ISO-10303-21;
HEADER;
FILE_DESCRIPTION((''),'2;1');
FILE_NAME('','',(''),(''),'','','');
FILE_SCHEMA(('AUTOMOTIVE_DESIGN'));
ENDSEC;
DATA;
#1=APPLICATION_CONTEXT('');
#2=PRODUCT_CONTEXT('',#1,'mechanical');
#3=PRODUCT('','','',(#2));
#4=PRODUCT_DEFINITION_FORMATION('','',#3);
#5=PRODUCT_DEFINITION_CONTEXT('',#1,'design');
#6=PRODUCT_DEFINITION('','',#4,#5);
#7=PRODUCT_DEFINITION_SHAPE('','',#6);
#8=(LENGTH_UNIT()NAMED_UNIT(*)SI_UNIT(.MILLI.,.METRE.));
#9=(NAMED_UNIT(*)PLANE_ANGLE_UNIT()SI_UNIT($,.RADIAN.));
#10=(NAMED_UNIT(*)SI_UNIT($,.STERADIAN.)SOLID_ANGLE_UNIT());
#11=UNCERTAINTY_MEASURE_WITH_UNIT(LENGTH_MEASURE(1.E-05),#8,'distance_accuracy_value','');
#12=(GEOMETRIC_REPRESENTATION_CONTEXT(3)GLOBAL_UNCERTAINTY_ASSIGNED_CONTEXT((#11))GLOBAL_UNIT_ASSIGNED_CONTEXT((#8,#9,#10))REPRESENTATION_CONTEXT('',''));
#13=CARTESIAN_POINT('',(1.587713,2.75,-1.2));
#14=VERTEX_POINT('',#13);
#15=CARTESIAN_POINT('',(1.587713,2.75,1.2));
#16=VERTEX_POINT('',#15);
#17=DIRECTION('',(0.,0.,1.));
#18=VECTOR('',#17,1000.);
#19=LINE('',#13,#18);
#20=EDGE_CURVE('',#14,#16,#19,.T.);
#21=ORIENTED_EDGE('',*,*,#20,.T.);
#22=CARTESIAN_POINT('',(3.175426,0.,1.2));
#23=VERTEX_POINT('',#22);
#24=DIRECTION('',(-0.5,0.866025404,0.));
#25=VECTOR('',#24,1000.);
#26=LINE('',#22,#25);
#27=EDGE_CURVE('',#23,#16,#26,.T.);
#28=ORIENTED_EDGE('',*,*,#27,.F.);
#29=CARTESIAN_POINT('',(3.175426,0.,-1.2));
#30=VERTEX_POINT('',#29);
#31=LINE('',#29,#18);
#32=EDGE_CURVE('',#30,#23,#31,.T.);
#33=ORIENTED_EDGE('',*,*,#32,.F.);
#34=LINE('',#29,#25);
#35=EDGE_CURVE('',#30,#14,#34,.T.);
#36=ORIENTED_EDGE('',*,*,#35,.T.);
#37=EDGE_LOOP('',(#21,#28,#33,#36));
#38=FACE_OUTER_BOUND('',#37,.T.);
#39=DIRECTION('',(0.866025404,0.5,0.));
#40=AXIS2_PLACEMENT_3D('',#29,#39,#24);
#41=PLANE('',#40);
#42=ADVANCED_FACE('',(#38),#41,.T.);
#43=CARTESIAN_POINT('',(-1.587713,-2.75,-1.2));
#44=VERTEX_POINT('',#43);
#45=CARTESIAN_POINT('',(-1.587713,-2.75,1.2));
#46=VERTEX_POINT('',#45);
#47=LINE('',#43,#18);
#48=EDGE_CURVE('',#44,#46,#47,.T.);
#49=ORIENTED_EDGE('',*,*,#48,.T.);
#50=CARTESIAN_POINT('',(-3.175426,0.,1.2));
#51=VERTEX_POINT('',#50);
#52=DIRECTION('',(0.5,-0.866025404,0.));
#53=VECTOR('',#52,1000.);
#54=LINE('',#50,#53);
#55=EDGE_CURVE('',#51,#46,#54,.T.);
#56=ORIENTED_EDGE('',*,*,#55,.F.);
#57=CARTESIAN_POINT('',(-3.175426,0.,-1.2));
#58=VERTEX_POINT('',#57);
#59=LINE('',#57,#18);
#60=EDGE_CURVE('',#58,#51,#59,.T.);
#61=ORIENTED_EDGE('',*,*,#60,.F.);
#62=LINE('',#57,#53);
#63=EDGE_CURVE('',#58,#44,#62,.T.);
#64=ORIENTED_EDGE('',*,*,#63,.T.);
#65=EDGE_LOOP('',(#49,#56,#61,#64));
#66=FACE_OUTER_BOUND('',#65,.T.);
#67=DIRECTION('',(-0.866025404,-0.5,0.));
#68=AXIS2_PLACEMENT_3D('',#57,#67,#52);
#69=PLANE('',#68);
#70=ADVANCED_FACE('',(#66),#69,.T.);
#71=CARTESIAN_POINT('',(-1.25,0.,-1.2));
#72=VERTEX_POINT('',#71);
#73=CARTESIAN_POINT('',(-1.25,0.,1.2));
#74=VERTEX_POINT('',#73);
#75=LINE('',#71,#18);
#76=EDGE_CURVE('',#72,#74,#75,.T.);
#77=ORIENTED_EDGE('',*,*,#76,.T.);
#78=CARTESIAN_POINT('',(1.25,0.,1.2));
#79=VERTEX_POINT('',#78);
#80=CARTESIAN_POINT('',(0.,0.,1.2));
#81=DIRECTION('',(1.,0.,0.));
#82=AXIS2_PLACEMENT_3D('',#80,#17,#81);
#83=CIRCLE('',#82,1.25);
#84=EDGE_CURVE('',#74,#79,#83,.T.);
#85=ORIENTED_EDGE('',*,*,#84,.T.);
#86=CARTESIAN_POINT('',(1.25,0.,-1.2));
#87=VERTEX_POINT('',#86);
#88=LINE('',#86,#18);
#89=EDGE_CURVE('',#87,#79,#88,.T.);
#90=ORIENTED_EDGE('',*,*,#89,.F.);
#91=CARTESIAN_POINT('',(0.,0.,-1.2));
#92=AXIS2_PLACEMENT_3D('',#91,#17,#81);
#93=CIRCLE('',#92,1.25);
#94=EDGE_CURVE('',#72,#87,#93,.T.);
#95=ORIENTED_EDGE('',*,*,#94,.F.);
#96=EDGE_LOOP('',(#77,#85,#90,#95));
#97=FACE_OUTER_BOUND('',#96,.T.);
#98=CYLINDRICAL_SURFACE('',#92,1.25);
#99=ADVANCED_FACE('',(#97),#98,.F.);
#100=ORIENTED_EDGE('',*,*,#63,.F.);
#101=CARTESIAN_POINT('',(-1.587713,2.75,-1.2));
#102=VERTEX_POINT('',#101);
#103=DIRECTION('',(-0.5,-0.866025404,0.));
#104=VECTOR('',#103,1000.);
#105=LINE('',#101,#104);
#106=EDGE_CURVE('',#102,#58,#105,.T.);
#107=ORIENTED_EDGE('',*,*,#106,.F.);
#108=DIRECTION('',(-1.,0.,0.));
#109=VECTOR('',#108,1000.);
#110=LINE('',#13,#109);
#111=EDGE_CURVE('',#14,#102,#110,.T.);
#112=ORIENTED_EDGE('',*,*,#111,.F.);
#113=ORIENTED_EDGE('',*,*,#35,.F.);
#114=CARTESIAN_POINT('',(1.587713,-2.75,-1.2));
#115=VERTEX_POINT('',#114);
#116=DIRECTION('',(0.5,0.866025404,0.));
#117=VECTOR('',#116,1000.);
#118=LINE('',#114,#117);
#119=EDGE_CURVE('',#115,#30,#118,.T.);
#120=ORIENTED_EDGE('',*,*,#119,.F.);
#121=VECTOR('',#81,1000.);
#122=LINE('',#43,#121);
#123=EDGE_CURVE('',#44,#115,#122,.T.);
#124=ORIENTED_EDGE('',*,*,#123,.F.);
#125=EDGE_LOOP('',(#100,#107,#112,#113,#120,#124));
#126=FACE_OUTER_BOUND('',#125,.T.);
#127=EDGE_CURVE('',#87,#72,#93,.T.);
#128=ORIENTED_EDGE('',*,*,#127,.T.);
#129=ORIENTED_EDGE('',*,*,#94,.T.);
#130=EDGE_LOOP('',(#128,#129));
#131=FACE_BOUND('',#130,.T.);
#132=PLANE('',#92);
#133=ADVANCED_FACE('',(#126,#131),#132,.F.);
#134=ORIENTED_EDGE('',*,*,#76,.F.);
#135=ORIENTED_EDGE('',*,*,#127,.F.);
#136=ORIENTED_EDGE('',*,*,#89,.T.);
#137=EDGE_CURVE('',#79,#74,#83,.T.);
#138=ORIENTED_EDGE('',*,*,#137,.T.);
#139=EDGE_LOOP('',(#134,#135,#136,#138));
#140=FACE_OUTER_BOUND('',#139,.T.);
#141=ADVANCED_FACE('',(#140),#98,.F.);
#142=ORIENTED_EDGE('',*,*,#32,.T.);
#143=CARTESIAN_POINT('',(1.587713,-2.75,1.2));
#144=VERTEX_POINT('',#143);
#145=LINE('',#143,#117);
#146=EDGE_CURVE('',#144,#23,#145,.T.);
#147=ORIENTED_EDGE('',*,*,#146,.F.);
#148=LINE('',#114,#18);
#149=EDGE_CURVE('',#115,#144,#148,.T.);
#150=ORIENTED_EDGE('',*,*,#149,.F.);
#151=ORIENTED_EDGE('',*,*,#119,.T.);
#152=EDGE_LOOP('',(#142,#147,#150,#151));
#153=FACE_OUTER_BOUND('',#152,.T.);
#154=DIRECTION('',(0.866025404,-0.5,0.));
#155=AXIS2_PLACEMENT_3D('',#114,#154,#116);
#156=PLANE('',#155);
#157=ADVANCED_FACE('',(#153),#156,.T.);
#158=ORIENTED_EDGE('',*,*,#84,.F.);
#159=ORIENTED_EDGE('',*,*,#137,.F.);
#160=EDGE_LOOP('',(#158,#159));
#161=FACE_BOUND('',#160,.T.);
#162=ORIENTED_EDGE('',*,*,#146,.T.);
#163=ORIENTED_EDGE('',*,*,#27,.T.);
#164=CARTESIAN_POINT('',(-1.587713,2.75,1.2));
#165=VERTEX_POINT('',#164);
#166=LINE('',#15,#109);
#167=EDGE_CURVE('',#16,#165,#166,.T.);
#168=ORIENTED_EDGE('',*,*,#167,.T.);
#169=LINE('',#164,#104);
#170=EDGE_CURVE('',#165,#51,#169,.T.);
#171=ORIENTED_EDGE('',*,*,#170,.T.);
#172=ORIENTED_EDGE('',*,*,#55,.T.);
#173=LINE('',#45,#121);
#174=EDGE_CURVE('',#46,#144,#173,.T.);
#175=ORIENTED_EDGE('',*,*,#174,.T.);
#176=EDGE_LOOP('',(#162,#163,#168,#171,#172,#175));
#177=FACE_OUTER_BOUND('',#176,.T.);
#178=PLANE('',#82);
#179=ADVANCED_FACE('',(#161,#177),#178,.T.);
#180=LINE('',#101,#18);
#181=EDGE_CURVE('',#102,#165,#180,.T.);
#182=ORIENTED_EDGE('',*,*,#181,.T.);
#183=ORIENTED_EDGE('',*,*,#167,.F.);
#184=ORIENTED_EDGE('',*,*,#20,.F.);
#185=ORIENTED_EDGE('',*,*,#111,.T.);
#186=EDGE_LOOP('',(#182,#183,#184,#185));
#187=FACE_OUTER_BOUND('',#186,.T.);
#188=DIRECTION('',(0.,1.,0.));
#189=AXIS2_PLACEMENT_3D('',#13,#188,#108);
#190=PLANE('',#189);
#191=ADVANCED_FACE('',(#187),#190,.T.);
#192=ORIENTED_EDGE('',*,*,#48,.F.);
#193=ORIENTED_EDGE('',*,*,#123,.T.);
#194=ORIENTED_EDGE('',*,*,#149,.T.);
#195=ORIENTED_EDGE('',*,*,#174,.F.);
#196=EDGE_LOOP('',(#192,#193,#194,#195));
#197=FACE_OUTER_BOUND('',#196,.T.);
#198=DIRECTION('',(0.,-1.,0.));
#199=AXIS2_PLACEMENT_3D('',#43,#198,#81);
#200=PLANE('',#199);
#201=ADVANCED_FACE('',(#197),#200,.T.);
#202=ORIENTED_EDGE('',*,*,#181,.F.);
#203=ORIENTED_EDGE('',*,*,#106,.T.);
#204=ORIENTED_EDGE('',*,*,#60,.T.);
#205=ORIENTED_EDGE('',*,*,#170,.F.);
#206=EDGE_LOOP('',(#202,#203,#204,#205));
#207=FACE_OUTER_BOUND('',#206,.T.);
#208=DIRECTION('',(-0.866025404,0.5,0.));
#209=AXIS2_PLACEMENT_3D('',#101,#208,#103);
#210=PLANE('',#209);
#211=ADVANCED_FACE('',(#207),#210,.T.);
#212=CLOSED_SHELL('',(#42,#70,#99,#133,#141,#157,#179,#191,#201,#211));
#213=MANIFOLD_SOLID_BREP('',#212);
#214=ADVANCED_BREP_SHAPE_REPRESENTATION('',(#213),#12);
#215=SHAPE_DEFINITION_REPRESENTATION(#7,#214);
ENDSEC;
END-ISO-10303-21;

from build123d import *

# Parameters (mm, degrees)
SKETCH_1_R      = 1.25
EXTRUDE_1_DEPTH = 1.2


with BuildPart() as part:
    # 草图1 → 凸台-拉伸1 (new, symmetric)
    with BuildSketch(Plane.XY):
        Polygon((3.175426481, 0), (1.58771324, 2.75), (-1.58771324, 2.75), (-3.175426481, 0), (-1.58771324, -2.75), (1.58771324, -2.75), align=None)
        Circle(SKETCH_1_R, mode=Mode.SUBTRACT)
    extrude(amount=EXTRUDE_1_DEPTH, both=True)


solid = part.part
